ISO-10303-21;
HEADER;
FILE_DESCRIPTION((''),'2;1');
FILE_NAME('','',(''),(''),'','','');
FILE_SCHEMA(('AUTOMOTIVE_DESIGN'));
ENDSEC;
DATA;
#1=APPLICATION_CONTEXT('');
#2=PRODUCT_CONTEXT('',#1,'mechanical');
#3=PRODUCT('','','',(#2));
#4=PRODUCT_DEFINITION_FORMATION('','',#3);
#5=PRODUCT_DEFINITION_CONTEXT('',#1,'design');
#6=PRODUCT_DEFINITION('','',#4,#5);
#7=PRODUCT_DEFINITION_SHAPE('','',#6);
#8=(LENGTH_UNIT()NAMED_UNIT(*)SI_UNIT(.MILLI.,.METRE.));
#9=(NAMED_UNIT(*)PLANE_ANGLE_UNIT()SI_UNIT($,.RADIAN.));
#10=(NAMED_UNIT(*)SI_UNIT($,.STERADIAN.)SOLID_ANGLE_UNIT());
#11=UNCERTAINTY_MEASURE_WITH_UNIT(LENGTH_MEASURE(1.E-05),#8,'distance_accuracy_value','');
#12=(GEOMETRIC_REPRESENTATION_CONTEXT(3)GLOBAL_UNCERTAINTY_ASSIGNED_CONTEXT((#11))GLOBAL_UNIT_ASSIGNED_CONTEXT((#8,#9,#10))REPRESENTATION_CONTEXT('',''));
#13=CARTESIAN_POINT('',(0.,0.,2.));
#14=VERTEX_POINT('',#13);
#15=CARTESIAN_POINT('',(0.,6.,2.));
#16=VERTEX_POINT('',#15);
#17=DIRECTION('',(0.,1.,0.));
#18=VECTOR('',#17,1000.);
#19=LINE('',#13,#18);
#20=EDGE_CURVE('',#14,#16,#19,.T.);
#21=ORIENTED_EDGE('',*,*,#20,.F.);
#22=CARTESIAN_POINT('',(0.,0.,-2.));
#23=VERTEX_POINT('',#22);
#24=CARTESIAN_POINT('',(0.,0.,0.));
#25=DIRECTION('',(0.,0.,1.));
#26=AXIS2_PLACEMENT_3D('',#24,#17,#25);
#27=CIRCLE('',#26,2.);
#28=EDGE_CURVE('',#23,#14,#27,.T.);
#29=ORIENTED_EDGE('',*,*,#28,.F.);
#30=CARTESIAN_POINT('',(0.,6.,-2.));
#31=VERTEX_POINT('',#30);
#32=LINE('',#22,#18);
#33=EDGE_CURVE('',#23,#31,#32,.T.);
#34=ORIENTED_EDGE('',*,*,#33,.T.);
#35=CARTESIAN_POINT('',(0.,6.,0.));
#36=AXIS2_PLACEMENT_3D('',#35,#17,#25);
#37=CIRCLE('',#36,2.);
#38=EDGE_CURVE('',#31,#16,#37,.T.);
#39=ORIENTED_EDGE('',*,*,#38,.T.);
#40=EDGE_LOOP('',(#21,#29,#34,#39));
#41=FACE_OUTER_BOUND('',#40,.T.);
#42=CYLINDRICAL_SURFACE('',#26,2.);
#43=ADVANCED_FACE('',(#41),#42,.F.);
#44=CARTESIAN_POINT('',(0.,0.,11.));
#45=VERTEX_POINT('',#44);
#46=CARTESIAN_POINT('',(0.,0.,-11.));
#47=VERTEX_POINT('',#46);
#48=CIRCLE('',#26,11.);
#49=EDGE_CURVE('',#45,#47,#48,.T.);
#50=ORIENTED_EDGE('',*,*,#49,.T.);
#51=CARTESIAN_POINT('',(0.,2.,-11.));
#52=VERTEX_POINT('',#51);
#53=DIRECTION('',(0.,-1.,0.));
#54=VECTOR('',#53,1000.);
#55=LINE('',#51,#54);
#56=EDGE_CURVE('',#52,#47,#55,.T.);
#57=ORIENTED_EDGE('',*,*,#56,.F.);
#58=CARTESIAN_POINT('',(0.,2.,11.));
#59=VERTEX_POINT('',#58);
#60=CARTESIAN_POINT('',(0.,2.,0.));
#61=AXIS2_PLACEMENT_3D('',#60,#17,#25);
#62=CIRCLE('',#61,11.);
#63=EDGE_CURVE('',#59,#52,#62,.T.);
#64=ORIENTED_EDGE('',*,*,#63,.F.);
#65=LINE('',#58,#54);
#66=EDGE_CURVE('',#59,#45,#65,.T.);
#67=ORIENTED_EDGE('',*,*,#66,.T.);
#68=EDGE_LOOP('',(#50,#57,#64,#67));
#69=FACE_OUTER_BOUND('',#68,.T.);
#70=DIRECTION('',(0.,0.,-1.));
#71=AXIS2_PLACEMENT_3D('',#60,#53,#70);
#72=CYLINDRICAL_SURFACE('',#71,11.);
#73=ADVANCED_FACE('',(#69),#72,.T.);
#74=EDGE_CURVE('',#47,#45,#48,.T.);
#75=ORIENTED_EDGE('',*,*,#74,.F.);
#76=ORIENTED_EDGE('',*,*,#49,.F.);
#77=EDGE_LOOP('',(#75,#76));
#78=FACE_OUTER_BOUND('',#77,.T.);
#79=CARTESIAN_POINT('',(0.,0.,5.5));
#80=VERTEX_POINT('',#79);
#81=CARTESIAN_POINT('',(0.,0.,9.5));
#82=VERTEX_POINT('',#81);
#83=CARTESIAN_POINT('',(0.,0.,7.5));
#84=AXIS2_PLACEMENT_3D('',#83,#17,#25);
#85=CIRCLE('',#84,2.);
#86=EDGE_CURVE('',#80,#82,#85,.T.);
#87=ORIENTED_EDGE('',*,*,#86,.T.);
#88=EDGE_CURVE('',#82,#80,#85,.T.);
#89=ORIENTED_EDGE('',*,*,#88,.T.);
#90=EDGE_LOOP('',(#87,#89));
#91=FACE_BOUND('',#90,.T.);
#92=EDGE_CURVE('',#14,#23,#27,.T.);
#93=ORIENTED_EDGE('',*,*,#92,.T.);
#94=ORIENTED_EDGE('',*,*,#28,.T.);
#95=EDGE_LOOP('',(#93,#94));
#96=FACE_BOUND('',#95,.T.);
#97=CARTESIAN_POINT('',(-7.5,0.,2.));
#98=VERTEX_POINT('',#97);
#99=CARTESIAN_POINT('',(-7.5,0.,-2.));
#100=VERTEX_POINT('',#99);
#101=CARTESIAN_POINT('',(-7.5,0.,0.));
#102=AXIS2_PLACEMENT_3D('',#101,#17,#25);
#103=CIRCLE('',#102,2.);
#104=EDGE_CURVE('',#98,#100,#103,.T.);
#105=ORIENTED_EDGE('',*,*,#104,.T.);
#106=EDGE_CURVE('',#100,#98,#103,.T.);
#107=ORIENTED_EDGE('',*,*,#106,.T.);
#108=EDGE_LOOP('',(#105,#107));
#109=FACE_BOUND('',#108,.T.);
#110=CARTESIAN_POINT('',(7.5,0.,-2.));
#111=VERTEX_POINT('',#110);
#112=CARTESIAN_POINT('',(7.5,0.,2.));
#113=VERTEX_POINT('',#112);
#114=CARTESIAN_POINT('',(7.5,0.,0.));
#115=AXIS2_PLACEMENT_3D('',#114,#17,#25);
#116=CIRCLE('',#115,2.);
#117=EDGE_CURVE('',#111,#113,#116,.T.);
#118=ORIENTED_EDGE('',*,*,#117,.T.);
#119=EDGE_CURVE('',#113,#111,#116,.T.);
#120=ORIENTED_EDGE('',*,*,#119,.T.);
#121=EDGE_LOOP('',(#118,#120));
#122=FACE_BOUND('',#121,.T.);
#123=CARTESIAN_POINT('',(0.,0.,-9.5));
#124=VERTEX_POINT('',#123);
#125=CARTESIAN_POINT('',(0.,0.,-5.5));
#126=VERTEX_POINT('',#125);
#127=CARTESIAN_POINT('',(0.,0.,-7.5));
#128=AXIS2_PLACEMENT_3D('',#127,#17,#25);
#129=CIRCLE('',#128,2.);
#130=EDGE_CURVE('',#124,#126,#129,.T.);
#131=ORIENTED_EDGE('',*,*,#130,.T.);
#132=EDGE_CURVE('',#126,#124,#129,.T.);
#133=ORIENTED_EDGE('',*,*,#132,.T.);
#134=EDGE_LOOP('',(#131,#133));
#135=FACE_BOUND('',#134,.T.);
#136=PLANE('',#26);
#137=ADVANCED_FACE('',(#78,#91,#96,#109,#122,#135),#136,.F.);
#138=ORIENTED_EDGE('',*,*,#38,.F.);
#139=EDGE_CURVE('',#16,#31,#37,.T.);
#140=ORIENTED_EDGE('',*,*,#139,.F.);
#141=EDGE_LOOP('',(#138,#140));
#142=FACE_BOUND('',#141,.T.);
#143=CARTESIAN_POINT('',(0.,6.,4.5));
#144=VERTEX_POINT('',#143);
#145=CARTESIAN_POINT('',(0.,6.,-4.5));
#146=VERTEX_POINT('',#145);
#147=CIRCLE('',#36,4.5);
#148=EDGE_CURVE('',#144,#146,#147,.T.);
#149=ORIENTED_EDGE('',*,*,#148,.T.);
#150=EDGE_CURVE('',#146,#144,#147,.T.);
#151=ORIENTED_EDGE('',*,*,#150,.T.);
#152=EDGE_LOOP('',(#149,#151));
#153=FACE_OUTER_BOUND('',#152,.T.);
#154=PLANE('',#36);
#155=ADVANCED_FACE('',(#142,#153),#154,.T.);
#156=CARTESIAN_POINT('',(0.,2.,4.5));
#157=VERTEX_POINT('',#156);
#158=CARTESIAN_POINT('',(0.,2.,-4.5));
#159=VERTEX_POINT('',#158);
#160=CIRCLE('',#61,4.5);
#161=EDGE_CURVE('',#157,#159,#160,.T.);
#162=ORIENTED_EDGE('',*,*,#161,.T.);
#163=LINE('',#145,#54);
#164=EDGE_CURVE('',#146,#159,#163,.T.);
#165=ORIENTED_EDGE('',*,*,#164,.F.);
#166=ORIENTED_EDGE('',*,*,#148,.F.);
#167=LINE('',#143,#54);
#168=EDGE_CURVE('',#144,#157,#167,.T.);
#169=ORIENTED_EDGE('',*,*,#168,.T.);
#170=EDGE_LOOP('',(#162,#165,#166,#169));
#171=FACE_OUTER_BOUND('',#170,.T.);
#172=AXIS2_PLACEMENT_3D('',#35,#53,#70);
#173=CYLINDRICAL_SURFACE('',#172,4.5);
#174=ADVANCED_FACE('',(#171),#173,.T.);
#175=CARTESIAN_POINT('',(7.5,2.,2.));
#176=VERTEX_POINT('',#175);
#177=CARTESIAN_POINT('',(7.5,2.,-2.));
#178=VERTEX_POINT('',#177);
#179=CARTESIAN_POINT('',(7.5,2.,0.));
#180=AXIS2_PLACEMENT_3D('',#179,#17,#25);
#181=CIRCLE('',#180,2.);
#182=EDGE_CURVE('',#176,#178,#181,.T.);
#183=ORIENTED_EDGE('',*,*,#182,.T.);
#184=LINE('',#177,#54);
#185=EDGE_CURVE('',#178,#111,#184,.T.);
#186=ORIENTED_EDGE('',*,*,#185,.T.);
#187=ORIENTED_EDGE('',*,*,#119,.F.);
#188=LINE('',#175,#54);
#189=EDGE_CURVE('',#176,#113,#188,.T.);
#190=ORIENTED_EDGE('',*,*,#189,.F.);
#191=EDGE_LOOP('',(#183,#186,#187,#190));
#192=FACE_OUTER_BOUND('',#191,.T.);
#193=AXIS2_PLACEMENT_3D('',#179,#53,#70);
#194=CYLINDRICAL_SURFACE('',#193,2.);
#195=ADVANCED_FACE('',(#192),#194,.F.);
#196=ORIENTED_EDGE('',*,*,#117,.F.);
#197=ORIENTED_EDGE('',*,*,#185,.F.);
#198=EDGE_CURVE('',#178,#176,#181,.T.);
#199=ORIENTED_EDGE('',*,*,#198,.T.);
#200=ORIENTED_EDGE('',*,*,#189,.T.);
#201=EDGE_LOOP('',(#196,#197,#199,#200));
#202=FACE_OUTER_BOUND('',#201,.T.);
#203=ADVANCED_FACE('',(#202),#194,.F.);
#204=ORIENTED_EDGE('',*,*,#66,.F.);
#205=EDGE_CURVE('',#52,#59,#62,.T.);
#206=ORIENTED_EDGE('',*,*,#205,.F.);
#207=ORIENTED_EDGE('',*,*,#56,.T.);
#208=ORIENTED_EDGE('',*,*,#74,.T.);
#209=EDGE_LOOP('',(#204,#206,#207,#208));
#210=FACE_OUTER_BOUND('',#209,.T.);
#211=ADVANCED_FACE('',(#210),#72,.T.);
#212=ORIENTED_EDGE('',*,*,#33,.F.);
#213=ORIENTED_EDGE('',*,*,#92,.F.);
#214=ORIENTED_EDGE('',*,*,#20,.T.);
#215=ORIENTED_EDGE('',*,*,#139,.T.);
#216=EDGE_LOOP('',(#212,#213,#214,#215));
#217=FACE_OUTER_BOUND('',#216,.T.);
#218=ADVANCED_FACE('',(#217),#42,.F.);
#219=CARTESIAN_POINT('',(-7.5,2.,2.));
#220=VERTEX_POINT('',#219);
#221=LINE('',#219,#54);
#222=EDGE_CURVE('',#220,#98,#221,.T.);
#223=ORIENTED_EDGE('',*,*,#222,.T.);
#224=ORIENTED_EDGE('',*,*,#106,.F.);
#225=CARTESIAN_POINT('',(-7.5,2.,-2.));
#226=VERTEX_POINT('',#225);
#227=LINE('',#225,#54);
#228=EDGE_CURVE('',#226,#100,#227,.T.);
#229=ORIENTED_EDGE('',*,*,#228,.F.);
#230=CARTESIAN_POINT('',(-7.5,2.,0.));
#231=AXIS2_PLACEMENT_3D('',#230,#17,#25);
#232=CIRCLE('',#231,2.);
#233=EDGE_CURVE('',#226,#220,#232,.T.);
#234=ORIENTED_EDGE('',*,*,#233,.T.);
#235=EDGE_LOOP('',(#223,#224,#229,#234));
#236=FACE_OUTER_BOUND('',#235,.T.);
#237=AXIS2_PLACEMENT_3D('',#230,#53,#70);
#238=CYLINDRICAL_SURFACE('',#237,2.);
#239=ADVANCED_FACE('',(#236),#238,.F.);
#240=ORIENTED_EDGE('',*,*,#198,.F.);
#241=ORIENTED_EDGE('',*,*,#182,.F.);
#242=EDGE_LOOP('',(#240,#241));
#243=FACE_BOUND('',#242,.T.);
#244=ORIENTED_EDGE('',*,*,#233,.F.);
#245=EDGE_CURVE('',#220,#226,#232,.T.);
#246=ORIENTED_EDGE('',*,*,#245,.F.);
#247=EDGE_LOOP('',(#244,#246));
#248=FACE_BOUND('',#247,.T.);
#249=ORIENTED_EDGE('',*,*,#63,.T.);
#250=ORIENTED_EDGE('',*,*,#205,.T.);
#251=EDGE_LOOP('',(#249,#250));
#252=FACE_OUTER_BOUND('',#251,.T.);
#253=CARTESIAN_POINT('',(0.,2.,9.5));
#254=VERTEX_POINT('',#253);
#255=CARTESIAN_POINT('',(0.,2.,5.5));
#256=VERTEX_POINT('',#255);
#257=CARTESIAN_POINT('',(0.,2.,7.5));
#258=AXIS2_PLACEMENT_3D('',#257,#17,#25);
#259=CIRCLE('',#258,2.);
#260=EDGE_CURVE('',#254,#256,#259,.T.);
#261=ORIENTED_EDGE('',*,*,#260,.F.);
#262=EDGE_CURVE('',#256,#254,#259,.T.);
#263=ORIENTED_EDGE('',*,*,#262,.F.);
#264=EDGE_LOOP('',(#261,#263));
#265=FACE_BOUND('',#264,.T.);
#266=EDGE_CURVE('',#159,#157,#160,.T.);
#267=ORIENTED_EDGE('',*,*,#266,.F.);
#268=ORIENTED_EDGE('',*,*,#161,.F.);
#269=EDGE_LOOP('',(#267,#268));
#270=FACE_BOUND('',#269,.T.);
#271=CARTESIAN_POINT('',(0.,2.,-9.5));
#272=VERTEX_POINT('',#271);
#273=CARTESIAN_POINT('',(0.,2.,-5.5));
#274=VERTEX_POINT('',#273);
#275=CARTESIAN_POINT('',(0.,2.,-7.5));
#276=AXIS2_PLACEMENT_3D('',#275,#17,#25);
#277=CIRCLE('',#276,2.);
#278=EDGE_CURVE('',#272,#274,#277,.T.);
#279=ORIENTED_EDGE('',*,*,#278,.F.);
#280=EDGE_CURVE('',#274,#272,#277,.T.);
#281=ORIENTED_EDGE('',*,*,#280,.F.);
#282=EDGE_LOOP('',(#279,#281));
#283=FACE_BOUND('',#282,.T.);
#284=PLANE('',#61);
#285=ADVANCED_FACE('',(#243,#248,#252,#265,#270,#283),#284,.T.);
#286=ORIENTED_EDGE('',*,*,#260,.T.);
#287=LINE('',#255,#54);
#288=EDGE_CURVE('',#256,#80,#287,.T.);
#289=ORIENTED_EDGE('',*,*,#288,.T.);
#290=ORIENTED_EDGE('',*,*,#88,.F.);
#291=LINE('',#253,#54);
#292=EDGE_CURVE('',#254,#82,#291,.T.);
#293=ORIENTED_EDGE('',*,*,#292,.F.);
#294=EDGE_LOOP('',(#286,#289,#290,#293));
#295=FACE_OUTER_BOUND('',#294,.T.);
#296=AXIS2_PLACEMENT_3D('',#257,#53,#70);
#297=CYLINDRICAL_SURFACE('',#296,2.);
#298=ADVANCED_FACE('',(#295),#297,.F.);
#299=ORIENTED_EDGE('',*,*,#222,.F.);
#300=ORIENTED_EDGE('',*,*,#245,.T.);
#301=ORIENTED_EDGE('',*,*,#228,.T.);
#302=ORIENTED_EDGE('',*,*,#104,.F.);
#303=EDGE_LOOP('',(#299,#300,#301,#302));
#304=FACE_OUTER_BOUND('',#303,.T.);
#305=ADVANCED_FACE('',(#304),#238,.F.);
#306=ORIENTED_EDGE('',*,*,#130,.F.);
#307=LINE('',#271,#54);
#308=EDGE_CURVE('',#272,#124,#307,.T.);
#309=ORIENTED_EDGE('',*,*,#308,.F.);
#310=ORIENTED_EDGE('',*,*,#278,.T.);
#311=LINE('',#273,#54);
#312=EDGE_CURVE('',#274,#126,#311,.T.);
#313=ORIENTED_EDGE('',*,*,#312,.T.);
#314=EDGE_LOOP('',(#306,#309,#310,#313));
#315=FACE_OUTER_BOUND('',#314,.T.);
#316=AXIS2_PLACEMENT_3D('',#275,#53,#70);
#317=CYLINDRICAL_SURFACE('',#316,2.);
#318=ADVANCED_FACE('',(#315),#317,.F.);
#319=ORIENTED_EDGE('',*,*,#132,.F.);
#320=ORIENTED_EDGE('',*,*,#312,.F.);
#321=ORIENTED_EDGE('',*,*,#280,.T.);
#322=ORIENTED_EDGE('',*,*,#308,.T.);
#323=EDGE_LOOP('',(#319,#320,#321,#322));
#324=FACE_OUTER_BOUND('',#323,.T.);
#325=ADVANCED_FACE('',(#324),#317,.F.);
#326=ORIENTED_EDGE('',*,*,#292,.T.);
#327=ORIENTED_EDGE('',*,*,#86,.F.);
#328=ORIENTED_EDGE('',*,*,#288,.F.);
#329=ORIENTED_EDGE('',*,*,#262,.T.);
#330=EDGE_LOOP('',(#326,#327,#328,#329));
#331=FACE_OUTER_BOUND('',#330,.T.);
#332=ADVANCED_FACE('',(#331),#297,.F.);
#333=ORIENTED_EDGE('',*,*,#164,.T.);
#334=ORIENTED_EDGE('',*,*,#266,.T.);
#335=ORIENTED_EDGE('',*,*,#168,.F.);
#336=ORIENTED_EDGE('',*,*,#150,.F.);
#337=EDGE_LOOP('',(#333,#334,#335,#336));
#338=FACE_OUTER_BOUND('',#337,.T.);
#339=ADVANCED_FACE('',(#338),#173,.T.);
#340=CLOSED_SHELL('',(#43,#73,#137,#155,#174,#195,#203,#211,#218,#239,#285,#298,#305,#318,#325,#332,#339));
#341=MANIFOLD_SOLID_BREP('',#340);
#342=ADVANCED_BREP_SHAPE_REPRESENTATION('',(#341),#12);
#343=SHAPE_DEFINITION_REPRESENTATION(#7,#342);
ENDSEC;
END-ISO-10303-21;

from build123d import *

# Parameters (mm, degrees)
SKETCH_1_R               = 11
SKETCH_1_R_2             = 2
EXTRUDE_1_DEPTH          = 2
SKETCH_2_R               = 4.5
EXTRUDE_2_DEPTH          = 4
CUT_EXTRUDE_1_DEPTH      = 17.673332001
CUT_EXTRUDE_1_DEPTH_BACK = 17.673332001
SKETCH_3_R               = 2


with BuildPart() as part:
    # 草图1 → 凸台-拉伸1 (new body)
    with BuildSketch(Plane(origin=(0, 0, 0), x_dir=(1, 0, 0), z_dir=(0, 1, 0))):
        with Locations(Location((0, 0, 0), (0, 0, 270))):
            Circle(SKETCH_1_R)
        with Locations(Location((0, 7.5, 0), (0, 0, 270))):
            Circle(SKETCH_1_R_2, mode=Mode.SUBTRACT)
        with Locations(Location((7.5, 0, 0), (0, 0, 270))):
            Circle(SKETCH_1_R_2, mode=Mode.SUBTRACT)
        with Locations(Location((0, -7.5, 0), (0, 0, 270))):
            Circle(SKETCH_1_R_2, mode=Mode.SUBTRACT)
        with Locations(Location((-7.5, 0, 0), (0, 0, 270))):
            Circle(SKETCH_1_R_2, mode=Mode.SUBTRACT)
    extrude(amount=EXTRUDE_1_DEPTH)

    # 草图2 → 凸台-拉伸2 (add)
    with BuildSketch(Plane(origin=(0, 2, 0), x_dir=(1, 0, 0), z_dir=(0, 1, 0))):
        with Locations(Location((0, 0, 0), (0, 0, 270))):
            Circle(SKETCH_2_R)
    extrude(amount=EXTRUDE_2_DEPTH)

    # 草图3 → 切除-拉伸1 (cut, two sides: drawn at the far end of the back side and taken through both)
    with BuildSketch(Plane(origin=(0, 6, 0), x_dir=(1, 0, 0), z_dir=(0, 1, 0)).offset(-CUT_EXTRUDE_1_DEPTH_BACK)):
        with Locations(Location((0, 0, 0), (0, 0, 270))):
            Circle(SKETCH_3_R)
    extrude(amount=CUT_EXTRUDE_1_DEPTH + CUT_EXTRUDE_1_DEPTH_BACK, mode=Mode.SUBTRACT)


solid = part.part
